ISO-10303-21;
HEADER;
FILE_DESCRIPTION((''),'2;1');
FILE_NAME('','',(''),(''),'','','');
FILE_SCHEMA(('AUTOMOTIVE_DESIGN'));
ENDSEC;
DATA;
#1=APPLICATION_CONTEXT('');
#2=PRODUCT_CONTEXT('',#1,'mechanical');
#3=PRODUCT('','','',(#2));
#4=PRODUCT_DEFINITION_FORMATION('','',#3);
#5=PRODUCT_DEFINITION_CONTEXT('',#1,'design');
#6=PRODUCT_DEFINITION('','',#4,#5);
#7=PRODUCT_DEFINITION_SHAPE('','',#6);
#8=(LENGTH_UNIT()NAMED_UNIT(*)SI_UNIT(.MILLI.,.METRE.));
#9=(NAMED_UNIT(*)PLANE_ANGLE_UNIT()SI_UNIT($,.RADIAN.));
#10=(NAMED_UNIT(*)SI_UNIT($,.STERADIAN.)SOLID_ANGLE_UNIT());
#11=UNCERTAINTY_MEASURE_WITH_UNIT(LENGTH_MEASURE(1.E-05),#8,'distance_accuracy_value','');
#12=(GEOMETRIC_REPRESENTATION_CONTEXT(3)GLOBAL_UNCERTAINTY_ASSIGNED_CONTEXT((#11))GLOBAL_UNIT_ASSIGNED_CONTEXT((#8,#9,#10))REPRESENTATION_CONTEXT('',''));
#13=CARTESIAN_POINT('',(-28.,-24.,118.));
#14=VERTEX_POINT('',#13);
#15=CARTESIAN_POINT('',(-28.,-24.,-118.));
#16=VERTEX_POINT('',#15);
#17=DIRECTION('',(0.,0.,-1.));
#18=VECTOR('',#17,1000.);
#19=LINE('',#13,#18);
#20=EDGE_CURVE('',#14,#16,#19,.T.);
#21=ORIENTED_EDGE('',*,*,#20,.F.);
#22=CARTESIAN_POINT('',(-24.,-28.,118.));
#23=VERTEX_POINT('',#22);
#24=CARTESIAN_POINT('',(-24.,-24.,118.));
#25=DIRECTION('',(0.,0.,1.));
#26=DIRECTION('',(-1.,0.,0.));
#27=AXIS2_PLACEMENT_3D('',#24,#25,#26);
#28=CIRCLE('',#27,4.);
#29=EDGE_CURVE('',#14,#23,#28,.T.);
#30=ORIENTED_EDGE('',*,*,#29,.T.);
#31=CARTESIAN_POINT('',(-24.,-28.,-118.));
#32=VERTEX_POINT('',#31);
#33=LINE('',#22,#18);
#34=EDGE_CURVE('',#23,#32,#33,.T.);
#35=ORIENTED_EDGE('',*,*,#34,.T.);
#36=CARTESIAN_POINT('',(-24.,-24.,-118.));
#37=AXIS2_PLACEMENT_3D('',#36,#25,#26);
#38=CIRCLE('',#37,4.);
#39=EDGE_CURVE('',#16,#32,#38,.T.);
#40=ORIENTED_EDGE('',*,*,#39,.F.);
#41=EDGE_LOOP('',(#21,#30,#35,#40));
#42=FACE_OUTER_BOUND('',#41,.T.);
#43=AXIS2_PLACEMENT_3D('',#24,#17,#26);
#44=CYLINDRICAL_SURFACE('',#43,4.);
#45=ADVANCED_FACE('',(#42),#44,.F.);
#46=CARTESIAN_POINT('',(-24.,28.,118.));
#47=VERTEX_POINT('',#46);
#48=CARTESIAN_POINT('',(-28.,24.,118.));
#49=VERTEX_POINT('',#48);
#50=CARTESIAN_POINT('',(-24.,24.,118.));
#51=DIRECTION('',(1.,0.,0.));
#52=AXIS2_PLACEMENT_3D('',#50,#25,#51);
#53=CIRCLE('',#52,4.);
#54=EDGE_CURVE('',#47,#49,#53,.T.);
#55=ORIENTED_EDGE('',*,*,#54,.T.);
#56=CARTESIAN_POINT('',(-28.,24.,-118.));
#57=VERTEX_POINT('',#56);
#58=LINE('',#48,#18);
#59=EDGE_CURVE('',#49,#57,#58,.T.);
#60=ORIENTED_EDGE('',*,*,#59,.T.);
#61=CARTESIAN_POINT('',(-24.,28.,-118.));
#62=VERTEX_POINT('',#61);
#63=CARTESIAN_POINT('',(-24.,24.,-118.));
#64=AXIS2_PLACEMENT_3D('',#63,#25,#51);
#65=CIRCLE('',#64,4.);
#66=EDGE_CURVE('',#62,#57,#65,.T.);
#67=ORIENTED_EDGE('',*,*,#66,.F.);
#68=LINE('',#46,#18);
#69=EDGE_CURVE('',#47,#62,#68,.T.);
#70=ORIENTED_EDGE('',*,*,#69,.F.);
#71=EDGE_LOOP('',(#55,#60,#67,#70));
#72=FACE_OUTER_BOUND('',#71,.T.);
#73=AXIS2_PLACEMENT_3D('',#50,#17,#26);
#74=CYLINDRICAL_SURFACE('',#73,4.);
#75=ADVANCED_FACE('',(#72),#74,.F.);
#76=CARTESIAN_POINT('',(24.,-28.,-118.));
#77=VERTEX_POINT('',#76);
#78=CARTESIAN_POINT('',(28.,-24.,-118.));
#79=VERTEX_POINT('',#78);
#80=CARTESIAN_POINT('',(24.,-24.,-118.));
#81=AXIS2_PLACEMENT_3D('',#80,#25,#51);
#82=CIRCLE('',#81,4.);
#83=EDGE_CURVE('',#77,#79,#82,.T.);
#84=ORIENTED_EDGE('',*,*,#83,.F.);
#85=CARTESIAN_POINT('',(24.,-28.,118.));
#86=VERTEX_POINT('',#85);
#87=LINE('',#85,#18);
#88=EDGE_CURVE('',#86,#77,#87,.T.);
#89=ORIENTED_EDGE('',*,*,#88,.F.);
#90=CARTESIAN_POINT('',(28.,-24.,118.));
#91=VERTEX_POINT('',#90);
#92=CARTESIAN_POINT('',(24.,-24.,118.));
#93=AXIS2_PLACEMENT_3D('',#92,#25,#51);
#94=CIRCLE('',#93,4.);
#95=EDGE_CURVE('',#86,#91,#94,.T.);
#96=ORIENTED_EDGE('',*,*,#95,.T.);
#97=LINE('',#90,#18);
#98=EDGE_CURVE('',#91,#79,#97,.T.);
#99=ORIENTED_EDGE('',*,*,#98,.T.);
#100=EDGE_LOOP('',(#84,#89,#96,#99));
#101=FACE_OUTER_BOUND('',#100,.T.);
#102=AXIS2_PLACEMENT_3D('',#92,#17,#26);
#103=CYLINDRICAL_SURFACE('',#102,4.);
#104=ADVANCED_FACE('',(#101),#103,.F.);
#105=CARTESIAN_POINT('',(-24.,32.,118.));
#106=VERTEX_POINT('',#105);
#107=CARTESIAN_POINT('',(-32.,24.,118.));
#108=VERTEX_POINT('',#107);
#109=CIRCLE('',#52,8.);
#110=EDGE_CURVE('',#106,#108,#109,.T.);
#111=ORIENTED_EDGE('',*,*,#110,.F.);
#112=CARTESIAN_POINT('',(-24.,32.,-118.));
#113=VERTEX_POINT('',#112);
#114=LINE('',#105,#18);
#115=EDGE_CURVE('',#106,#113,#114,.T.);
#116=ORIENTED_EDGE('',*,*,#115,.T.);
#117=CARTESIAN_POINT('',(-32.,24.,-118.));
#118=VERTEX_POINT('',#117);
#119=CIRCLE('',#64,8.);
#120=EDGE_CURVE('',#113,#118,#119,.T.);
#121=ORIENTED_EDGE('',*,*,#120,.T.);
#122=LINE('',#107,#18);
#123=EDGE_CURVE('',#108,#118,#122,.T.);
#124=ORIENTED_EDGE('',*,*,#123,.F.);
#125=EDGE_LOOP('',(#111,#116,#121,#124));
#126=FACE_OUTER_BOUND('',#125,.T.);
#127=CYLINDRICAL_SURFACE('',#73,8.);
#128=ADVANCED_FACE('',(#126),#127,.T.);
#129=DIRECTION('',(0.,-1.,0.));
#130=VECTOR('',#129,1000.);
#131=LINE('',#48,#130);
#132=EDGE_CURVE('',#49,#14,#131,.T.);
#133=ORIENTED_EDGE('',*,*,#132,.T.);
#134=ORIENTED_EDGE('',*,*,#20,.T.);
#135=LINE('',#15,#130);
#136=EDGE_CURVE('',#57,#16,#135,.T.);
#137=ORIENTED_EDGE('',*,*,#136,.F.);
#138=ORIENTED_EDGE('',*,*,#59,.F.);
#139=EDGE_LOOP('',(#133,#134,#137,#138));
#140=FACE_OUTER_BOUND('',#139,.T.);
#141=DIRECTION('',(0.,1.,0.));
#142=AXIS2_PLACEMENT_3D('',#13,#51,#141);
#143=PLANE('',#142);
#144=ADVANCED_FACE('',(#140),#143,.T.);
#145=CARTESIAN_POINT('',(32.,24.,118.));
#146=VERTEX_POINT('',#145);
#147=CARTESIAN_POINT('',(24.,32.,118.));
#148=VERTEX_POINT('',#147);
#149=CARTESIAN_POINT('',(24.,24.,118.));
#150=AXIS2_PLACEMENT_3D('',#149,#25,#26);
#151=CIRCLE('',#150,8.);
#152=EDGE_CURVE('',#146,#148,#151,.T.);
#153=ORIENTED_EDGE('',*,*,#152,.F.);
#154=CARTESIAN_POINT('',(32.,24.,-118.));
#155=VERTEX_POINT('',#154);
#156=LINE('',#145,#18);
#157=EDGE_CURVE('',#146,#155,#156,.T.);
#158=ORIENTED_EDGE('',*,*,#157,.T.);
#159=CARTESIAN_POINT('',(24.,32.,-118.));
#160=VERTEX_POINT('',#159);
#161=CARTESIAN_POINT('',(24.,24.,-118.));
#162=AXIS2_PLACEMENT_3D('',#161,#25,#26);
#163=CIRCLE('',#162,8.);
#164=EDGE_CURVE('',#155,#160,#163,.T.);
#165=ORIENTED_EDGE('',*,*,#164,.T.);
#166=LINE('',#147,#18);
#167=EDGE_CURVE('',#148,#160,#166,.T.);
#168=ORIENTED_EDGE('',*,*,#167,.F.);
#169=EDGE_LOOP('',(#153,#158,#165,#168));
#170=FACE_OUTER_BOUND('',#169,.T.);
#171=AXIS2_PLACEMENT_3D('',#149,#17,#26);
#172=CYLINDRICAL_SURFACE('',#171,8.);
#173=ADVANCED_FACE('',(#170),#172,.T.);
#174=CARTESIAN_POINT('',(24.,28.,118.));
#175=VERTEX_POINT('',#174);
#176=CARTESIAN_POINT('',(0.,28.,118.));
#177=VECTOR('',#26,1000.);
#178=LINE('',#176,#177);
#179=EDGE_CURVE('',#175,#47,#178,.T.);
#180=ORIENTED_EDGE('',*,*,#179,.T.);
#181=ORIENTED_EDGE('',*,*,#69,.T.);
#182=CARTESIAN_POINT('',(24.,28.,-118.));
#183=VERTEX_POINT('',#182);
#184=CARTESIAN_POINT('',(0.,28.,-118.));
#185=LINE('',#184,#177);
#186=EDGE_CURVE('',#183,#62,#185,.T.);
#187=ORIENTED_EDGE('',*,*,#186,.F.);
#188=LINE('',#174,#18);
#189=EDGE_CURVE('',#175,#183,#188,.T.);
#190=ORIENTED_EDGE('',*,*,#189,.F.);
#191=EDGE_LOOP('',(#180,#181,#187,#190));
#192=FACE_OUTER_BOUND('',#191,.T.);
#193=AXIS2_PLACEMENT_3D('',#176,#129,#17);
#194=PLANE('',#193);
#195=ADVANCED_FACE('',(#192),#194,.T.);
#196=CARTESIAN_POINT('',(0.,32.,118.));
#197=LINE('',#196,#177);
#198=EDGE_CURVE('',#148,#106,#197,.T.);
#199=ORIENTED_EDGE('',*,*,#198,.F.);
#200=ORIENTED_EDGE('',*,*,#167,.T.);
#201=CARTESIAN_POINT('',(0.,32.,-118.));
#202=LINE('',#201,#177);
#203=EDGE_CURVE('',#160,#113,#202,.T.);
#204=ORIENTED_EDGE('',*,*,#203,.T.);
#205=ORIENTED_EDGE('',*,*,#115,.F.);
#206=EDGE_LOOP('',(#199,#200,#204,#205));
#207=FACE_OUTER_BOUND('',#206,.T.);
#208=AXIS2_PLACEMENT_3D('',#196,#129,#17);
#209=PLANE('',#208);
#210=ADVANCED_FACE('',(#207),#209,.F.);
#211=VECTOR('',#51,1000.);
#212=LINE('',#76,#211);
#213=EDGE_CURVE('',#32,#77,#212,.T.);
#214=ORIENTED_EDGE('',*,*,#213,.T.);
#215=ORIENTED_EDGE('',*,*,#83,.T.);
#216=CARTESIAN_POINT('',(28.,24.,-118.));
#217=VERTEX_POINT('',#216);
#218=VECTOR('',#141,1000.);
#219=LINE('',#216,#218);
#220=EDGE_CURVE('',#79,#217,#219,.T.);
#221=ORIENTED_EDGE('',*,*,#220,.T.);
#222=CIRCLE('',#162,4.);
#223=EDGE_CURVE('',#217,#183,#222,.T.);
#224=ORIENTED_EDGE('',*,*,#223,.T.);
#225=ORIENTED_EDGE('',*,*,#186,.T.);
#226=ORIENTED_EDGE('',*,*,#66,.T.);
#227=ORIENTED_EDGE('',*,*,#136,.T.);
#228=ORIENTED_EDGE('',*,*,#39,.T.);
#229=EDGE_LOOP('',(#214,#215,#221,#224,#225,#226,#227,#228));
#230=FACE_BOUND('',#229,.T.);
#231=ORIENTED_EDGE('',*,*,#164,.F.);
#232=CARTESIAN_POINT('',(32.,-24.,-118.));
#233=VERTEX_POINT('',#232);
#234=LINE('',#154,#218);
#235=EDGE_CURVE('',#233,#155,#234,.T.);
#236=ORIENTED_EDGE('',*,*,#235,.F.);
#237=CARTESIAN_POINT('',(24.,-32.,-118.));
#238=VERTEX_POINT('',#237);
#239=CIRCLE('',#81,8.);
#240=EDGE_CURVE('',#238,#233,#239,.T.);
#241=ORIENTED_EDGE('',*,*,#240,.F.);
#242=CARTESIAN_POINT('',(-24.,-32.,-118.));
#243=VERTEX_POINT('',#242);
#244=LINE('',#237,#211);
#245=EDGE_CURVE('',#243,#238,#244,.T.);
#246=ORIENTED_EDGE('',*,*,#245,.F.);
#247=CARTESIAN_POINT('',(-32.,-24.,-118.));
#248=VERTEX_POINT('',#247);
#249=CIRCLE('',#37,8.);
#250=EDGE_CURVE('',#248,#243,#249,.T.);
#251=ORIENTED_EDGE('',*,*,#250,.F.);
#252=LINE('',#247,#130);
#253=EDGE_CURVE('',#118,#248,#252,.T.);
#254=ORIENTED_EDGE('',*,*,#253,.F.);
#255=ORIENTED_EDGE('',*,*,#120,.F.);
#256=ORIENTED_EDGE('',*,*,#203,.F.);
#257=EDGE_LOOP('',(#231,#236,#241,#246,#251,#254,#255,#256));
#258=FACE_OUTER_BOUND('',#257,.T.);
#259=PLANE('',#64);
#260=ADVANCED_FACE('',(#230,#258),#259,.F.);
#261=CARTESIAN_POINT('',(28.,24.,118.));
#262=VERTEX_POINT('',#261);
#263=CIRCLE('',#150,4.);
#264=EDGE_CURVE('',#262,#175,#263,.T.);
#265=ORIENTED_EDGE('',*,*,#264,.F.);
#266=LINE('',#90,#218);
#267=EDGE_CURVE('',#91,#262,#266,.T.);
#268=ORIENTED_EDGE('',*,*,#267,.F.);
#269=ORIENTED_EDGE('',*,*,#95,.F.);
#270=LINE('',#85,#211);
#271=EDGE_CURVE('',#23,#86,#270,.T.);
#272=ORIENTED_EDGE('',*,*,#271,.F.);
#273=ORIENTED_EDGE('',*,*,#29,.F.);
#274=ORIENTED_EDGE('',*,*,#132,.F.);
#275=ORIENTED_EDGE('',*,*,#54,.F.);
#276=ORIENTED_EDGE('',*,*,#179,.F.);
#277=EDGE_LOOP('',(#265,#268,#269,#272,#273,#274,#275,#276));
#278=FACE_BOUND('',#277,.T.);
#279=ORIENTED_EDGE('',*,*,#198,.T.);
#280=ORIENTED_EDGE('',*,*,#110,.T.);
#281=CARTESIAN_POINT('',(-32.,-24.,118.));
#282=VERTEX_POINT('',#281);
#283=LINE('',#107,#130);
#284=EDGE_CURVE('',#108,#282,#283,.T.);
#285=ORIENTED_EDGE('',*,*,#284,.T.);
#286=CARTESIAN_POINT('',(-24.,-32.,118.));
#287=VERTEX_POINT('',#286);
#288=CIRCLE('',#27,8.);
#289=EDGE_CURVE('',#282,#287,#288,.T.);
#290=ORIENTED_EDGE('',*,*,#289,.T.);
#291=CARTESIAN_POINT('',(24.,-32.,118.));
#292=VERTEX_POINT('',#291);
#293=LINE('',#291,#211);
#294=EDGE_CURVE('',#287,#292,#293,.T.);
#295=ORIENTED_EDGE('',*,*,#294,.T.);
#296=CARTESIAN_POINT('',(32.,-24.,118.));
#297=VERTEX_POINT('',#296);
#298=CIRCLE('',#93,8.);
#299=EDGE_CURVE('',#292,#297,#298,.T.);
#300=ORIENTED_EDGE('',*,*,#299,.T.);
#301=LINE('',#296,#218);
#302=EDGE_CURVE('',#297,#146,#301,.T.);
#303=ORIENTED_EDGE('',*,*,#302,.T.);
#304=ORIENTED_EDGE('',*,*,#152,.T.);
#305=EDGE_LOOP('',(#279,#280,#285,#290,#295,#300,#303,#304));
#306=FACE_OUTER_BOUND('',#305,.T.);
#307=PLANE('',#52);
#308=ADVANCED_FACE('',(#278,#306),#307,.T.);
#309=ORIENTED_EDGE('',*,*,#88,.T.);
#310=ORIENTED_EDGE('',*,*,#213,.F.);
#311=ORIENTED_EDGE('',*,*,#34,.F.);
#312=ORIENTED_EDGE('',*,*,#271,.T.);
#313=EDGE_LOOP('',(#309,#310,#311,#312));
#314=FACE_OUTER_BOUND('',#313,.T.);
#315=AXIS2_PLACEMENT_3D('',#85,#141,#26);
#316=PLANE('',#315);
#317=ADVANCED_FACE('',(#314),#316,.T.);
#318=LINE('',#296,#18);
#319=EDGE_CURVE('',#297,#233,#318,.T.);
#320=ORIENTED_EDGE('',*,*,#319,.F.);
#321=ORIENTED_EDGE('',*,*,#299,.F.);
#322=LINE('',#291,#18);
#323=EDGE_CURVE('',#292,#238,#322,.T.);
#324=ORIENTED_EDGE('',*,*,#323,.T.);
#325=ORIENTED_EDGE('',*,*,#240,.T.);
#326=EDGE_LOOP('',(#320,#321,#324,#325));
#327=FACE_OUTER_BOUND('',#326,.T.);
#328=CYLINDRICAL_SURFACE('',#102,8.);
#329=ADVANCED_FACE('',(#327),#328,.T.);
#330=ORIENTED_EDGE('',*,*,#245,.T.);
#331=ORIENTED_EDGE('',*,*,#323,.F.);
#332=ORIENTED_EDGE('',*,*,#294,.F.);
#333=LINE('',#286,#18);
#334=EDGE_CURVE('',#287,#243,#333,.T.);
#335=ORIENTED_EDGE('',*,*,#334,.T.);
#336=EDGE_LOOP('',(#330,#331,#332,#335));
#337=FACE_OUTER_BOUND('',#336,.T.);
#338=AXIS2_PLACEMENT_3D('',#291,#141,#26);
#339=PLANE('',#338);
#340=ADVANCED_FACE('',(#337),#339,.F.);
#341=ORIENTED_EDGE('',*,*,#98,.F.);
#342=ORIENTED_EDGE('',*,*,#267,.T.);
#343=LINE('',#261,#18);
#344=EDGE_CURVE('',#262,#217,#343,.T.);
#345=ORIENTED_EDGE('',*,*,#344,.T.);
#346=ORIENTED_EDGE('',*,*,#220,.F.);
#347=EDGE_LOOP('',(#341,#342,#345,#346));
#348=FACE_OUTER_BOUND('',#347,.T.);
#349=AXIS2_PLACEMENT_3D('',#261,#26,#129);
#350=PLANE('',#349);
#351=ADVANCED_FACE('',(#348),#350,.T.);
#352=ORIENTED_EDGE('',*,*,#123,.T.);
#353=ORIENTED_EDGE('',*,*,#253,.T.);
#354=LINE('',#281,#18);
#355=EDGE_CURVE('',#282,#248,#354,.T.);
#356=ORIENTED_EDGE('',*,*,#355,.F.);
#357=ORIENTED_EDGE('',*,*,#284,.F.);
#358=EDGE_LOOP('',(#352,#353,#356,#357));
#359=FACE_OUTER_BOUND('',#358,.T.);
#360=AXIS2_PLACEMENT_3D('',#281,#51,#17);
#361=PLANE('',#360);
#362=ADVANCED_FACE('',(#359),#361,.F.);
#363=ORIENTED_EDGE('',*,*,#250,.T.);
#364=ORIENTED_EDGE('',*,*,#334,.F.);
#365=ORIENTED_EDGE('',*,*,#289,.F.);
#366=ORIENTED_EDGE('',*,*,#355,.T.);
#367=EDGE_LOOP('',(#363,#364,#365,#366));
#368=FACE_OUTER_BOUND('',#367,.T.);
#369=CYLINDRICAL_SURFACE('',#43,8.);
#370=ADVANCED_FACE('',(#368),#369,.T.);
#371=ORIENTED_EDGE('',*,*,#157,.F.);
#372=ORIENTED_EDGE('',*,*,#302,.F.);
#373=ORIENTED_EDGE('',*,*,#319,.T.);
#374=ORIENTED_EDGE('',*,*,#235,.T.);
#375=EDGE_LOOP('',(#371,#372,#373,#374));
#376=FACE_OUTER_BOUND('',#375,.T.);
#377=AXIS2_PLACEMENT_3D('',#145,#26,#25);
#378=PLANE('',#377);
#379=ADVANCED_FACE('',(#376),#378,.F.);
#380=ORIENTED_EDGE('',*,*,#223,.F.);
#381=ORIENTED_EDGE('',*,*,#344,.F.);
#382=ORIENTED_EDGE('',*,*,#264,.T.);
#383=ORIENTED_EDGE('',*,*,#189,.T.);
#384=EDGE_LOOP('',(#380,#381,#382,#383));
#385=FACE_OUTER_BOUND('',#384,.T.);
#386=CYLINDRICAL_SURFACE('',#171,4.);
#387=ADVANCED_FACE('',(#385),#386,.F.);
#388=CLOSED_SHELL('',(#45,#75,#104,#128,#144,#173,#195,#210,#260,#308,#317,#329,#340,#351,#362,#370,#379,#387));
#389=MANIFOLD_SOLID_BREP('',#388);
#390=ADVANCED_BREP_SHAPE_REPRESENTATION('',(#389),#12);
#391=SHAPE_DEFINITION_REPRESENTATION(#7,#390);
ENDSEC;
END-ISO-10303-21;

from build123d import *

# Parameters (mm, degrees)
BOSS_EXTRUDE_1_DEPTH = 118


with BuildPart() as part:
    # Sketch 1 → Boss-Extrude 1 (new, symmetric)
    with BuildSketch(Plane.XY):
        with BuildLine():
            Line((0, 32), (-24, 32))
            ThreePointArc((-24, 32), (-29.656854249, 29.656854249), (-32, 24))
            Line((-32, 24), (-32, 0))
            Line((-32, 0), (-32, -24))
            ThreePointArc((-32, -24), (-29.656854249, -29.656854249), (-24, -32))
            Line((-24, -32), (24, -32))
            ThreePointArc((24, -32), (29.656854249, -29.656854249), (32, -24))
            Line((32, -24), (32, 0))
            Line((32, 0), (32, 24))
            ThreePointArc((32, 24), (29.656854249, 29.656854249), (24, 32))
            Line((24, 32), (0, 32))
        make_face()
        with BuildLine():
            Line((0, 28), (-24, 28))
            ThreePointArc((-24, 28), (-26.828427125, 26.828427125), (-28, 24))
            Line((-28, 24), (-28, 0))
            Line((-28, 0), (-28, -24))
            ThreePointArc((-28, -24), (-26.828427125, -26.828427125), (-24, -28))
            Line((-24, -28), (24, -28))
            ThreePointArc((24, -28), (26.828427125, -26.828427125), (28, -24))
            Line((28, -24), (28, 0))
            Line((28, 0), (28, 24))
            ThreePointArc((28, 24), (26.828427125, 26.828427125), (24, 28))
            Line((24, 28), (0, 28))
        make_face(mode=Mode.SUBTRACT)
    extrude(amount=BOSS_EXTRUDE_1_DEPTH, both=True)


solid = part.part
